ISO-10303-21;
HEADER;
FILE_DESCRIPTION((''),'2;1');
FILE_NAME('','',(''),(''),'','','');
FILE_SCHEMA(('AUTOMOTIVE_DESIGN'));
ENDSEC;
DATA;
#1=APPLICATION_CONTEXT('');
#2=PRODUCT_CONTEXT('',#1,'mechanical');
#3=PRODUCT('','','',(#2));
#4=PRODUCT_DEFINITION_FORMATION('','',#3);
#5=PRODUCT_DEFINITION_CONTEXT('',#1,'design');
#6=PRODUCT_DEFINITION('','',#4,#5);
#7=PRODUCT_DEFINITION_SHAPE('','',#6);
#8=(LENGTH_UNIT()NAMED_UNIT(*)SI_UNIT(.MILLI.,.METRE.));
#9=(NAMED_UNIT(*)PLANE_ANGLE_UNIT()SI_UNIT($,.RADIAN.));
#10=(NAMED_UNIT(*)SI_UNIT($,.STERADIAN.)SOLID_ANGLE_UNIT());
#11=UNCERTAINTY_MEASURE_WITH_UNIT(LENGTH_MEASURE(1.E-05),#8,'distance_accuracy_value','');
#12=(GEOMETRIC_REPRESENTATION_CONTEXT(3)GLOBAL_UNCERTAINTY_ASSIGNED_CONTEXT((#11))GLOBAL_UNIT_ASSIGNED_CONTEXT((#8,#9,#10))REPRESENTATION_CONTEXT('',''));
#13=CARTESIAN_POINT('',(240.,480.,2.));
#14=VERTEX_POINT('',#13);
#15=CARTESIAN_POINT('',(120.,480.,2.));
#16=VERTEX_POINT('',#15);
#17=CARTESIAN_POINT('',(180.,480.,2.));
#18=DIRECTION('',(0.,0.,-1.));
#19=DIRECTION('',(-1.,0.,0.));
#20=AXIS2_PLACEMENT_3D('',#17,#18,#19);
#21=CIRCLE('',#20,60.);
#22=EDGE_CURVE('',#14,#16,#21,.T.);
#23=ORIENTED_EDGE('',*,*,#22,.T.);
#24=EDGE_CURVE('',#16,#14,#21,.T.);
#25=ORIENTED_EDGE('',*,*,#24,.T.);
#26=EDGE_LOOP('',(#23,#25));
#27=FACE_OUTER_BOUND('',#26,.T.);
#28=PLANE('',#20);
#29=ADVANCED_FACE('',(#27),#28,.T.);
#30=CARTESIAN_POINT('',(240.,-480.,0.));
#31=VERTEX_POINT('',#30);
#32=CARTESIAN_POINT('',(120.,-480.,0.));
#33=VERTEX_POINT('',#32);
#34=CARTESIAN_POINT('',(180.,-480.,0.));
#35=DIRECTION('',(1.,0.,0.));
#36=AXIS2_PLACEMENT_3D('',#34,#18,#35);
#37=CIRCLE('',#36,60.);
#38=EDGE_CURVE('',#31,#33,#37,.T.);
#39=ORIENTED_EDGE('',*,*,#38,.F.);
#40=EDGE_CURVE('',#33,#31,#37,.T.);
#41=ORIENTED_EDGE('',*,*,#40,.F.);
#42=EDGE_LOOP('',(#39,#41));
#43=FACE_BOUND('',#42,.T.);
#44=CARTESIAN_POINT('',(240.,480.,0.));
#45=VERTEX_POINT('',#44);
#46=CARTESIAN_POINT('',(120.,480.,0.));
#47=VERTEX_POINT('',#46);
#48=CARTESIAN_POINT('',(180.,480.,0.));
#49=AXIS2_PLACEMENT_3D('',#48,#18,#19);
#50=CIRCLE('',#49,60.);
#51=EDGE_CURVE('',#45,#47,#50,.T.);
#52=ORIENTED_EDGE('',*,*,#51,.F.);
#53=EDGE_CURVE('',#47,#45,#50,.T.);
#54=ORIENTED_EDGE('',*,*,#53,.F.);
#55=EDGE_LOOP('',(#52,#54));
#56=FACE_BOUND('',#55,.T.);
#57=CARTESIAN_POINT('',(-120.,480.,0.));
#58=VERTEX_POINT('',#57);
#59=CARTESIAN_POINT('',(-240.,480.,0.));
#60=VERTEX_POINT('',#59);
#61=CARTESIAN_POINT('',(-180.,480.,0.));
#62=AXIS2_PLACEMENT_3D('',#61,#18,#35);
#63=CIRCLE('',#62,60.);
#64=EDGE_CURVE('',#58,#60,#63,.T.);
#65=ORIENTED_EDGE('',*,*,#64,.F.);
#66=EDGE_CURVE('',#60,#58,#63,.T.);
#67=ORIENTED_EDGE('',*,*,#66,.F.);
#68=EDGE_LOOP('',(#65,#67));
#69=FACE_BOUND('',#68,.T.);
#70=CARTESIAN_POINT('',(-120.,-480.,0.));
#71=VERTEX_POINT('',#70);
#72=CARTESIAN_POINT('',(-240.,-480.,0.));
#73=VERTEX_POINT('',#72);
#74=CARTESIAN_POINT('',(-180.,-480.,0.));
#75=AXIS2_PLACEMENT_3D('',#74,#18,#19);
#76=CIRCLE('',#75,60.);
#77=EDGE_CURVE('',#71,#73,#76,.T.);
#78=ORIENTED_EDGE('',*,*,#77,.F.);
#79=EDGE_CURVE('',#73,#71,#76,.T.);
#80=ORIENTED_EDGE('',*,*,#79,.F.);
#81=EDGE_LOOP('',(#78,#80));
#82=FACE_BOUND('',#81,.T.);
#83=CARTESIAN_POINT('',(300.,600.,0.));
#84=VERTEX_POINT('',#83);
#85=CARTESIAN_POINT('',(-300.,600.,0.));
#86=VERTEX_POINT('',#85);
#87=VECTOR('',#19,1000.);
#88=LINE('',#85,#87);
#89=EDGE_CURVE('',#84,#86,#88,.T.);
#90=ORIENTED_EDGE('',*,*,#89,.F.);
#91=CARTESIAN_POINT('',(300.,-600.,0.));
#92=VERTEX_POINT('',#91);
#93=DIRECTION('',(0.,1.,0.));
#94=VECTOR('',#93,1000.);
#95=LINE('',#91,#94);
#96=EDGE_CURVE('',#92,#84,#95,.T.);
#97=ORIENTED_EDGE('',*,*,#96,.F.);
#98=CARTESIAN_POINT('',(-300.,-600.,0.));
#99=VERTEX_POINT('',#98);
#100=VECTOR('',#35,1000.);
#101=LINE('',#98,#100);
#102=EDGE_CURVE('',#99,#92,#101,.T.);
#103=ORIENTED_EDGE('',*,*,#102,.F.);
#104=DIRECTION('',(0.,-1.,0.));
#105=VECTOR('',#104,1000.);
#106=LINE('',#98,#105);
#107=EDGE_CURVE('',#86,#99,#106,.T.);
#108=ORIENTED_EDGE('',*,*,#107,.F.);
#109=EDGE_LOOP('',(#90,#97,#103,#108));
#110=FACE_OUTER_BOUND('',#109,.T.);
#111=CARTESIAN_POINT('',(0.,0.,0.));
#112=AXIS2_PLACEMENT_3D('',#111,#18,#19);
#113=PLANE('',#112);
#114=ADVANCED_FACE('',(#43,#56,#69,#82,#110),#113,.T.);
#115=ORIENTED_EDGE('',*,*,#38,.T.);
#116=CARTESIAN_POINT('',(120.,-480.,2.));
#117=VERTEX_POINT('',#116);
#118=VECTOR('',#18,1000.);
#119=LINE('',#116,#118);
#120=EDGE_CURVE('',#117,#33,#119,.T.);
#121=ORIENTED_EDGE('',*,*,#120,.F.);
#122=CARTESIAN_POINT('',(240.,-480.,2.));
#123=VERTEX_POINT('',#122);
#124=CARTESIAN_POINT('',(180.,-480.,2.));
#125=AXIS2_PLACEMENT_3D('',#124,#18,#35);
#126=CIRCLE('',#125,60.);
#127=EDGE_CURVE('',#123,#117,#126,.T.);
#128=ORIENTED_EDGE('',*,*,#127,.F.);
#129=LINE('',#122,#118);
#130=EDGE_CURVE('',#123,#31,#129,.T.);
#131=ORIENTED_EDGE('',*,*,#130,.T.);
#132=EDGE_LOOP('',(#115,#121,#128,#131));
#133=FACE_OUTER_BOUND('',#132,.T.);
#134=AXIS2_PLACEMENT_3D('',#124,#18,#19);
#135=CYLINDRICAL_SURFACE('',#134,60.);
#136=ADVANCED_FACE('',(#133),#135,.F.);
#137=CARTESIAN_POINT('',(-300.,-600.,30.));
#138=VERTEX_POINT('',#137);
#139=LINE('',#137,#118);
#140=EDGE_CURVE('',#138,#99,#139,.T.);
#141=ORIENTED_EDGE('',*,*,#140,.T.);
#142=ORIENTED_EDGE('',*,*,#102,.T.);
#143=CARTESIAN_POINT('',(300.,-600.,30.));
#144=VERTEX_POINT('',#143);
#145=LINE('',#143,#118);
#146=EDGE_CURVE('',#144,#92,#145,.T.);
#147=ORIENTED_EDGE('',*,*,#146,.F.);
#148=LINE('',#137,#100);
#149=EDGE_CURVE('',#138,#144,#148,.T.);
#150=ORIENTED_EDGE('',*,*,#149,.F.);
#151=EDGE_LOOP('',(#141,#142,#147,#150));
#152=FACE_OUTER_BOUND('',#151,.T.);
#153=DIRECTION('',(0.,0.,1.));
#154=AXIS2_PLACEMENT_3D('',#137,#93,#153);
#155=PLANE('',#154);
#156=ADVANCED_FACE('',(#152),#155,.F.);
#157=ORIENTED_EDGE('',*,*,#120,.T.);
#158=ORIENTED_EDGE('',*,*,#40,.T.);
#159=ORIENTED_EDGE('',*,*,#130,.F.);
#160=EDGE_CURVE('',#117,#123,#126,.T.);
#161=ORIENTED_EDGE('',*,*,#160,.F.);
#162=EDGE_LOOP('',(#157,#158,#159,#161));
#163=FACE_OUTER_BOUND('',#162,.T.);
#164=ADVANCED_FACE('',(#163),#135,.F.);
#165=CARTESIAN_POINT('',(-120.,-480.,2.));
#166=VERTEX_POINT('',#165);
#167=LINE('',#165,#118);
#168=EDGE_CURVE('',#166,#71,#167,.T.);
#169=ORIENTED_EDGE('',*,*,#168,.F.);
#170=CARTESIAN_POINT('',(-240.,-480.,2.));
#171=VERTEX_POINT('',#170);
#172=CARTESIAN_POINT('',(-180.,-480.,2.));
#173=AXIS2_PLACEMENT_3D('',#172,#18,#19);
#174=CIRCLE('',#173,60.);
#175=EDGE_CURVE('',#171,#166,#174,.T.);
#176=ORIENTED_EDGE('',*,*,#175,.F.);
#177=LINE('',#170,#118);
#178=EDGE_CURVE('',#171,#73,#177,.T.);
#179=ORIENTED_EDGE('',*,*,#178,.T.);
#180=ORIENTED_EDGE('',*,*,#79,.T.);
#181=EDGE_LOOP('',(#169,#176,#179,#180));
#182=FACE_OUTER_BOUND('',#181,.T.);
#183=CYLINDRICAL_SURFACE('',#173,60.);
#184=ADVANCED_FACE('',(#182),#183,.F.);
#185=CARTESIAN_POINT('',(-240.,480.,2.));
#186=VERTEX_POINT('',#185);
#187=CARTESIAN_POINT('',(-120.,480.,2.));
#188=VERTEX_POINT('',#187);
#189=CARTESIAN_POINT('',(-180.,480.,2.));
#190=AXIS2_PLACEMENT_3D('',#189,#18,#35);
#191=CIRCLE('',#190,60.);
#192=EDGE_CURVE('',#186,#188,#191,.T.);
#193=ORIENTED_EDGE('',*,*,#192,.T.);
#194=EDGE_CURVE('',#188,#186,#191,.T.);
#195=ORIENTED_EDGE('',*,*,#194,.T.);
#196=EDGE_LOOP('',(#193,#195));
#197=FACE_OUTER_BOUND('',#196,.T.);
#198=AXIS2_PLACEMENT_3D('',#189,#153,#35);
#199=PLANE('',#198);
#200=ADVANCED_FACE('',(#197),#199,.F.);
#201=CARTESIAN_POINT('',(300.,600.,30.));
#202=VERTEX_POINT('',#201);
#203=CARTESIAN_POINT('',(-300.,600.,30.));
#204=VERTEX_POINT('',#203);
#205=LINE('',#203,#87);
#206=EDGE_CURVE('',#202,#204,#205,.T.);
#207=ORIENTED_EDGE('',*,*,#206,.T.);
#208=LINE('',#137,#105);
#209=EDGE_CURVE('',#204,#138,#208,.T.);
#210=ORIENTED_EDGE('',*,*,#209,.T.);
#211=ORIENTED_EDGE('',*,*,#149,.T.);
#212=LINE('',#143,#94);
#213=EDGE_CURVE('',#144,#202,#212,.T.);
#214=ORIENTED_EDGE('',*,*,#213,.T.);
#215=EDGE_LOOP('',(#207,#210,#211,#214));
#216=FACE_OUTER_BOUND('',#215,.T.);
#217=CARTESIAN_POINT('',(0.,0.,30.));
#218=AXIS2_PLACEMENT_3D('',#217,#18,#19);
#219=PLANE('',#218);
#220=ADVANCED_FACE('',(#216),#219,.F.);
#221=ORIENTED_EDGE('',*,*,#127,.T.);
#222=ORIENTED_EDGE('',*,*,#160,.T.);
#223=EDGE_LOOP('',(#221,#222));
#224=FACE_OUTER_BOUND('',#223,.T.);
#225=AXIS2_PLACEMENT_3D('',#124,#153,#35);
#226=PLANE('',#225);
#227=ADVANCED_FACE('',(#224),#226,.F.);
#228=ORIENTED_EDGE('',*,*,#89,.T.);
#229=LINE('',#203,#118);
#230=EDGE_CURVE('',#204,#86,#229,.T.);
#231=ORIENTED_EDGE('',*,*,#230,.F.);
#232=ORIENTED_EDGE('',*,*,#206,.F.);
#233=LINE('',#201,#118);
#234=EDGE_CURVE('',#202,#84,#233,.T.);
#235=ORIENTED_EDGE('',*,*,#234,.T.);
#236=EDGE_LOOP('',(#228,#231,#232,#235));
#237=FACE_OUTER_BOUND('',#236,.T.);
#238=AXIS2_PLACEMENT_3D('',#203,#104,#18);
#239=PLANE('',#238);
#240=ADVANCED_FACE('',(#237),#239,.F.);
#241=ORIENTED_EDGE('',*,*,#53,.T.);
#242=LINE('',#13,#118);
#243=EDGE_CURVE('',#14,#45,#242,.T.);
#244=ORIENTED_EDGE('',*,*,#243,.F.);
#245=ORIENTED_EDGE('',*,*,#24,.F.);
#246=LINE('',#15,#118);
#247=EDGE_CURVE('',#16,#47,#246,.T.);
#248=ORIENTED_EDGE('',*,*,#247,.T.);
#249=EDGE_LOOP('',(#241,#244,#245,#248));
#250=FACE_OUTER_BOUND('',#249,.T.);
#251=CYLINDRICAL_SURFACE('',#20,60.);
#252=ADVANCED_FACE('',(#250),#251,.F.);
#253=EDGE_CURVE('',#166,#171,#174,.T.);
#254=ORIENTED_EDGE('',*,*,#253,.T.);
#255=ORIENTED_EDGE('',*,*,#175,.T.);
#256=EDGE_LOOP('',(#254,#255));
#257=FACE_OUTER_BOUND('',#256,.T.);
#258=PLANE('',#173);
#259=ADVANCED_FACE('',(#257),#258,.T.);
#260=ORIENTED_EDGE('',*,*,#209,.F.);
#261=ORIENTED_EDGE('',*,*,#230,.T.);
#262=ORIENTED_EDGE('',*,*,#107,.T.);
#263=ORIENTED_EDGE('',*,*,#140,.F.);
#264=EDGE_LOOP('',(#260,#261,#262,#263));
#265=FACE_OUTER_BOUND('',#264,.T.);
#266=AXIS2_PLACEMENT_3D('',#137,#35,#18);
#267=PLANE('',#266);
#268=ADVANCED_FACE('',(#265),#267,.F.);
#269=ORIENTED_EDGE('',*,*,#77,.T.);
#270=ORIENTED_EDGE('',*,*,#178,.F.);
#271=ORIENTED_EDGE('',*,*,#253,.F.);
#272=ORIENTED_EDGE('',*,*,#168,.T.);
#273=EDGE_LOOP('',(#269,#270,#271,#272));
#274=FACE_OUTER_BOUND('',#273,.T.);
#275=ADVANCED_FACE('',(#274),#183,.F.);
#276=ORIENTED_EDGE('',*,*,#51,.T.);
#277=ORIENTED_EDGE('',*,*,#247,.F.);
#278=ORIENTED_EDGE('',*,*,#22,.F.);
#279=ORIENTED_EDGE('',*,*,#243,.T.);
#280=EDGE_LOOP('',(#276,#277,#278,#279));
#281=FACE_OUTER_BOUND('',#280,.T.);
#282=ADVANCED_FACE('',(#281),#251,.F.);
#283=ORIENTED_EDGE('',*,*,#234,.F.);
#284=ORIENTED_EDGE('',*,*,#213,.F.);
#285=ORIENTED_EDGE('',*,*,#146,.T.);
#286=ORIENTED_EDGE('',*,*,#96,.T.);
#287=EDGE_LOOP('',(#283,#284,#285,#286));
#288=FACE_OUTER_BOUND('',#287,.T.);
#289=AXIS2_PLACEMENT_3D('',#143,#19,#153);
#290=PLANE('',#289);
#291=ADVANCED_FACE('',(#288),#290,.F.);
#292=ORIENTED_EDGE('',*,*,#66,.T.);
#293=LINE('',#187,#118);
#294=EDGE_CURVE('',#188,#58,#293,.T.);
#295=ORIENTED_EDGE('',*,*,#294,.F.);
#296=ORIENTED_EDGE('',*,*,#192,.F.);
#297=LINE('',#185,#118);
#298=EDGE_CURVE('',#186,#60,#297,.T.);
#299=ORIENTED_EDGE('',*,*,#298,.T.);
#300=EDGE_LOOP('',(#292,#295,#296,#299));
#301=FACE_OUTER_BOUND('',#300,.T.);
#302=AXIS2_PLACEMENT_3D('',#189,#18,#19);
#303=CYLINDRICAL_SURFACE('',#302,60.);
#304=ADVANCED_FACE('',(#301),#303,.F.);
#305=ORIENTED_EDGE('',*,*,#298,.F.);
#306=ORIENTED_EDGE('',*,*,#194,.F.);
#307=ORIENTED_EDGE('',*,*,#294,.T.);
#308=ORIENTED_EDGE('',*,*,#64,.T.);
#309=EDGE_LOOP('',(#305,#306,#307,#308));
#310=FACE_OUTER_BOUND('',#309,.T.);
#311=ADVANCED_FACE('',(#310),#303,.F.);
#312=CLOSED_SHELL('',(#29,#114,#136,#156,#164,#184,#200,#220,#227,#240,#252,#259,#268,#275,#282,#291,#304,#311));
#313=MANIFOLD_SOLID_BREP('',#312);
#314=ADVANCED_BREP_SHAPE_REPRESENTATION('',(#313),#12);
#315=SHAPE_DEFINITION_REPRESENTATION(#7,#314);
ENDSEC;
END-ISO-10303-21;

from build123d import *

# Parameters (mm, degrees)
SKETCH1_W           = 600
SKETCH1_H           = 1200
BOSS_EXTRUDE1_DEPTH = 30
SKETCH2_R           = 60
CUT_EXTRUDE1_DEPTH  = 2


with BuildPart() as part:
    # Sketch1 → Boss-Extrude1 (new body)
    with BuildSketch(Plane.XY):
        Rectangle(SKETCH1_W, SKETCH1_H)
    extrude(amount=BOSS_EXTRUDE1_DEPTH)

    # Sketch2 → Cut-Extrude1 (cut)
    with BuildSketch(Plane(origin=(0, 0, 0), x_dir=(-1, 0, 0), z_dir=(0, 0, -1))):
        with Locations((-180, 480)):
            Circle(SKETCH2_R)
        with Locations(Location((180, 480, 0), (0, 0, 180))):
            Circle(SKETCH2_R)
        with Locations((180, -480)):
            Circle(SKETCH2_R)
        with Locations(Location((-180, -480, 0), (0, 0, 180))):
            Circle(SKETCH2_R)
    extrude(amount=-CUT_EXTRUDE1_DEPTH, mode=Mode.SUBTRACT)


solid = part.part
